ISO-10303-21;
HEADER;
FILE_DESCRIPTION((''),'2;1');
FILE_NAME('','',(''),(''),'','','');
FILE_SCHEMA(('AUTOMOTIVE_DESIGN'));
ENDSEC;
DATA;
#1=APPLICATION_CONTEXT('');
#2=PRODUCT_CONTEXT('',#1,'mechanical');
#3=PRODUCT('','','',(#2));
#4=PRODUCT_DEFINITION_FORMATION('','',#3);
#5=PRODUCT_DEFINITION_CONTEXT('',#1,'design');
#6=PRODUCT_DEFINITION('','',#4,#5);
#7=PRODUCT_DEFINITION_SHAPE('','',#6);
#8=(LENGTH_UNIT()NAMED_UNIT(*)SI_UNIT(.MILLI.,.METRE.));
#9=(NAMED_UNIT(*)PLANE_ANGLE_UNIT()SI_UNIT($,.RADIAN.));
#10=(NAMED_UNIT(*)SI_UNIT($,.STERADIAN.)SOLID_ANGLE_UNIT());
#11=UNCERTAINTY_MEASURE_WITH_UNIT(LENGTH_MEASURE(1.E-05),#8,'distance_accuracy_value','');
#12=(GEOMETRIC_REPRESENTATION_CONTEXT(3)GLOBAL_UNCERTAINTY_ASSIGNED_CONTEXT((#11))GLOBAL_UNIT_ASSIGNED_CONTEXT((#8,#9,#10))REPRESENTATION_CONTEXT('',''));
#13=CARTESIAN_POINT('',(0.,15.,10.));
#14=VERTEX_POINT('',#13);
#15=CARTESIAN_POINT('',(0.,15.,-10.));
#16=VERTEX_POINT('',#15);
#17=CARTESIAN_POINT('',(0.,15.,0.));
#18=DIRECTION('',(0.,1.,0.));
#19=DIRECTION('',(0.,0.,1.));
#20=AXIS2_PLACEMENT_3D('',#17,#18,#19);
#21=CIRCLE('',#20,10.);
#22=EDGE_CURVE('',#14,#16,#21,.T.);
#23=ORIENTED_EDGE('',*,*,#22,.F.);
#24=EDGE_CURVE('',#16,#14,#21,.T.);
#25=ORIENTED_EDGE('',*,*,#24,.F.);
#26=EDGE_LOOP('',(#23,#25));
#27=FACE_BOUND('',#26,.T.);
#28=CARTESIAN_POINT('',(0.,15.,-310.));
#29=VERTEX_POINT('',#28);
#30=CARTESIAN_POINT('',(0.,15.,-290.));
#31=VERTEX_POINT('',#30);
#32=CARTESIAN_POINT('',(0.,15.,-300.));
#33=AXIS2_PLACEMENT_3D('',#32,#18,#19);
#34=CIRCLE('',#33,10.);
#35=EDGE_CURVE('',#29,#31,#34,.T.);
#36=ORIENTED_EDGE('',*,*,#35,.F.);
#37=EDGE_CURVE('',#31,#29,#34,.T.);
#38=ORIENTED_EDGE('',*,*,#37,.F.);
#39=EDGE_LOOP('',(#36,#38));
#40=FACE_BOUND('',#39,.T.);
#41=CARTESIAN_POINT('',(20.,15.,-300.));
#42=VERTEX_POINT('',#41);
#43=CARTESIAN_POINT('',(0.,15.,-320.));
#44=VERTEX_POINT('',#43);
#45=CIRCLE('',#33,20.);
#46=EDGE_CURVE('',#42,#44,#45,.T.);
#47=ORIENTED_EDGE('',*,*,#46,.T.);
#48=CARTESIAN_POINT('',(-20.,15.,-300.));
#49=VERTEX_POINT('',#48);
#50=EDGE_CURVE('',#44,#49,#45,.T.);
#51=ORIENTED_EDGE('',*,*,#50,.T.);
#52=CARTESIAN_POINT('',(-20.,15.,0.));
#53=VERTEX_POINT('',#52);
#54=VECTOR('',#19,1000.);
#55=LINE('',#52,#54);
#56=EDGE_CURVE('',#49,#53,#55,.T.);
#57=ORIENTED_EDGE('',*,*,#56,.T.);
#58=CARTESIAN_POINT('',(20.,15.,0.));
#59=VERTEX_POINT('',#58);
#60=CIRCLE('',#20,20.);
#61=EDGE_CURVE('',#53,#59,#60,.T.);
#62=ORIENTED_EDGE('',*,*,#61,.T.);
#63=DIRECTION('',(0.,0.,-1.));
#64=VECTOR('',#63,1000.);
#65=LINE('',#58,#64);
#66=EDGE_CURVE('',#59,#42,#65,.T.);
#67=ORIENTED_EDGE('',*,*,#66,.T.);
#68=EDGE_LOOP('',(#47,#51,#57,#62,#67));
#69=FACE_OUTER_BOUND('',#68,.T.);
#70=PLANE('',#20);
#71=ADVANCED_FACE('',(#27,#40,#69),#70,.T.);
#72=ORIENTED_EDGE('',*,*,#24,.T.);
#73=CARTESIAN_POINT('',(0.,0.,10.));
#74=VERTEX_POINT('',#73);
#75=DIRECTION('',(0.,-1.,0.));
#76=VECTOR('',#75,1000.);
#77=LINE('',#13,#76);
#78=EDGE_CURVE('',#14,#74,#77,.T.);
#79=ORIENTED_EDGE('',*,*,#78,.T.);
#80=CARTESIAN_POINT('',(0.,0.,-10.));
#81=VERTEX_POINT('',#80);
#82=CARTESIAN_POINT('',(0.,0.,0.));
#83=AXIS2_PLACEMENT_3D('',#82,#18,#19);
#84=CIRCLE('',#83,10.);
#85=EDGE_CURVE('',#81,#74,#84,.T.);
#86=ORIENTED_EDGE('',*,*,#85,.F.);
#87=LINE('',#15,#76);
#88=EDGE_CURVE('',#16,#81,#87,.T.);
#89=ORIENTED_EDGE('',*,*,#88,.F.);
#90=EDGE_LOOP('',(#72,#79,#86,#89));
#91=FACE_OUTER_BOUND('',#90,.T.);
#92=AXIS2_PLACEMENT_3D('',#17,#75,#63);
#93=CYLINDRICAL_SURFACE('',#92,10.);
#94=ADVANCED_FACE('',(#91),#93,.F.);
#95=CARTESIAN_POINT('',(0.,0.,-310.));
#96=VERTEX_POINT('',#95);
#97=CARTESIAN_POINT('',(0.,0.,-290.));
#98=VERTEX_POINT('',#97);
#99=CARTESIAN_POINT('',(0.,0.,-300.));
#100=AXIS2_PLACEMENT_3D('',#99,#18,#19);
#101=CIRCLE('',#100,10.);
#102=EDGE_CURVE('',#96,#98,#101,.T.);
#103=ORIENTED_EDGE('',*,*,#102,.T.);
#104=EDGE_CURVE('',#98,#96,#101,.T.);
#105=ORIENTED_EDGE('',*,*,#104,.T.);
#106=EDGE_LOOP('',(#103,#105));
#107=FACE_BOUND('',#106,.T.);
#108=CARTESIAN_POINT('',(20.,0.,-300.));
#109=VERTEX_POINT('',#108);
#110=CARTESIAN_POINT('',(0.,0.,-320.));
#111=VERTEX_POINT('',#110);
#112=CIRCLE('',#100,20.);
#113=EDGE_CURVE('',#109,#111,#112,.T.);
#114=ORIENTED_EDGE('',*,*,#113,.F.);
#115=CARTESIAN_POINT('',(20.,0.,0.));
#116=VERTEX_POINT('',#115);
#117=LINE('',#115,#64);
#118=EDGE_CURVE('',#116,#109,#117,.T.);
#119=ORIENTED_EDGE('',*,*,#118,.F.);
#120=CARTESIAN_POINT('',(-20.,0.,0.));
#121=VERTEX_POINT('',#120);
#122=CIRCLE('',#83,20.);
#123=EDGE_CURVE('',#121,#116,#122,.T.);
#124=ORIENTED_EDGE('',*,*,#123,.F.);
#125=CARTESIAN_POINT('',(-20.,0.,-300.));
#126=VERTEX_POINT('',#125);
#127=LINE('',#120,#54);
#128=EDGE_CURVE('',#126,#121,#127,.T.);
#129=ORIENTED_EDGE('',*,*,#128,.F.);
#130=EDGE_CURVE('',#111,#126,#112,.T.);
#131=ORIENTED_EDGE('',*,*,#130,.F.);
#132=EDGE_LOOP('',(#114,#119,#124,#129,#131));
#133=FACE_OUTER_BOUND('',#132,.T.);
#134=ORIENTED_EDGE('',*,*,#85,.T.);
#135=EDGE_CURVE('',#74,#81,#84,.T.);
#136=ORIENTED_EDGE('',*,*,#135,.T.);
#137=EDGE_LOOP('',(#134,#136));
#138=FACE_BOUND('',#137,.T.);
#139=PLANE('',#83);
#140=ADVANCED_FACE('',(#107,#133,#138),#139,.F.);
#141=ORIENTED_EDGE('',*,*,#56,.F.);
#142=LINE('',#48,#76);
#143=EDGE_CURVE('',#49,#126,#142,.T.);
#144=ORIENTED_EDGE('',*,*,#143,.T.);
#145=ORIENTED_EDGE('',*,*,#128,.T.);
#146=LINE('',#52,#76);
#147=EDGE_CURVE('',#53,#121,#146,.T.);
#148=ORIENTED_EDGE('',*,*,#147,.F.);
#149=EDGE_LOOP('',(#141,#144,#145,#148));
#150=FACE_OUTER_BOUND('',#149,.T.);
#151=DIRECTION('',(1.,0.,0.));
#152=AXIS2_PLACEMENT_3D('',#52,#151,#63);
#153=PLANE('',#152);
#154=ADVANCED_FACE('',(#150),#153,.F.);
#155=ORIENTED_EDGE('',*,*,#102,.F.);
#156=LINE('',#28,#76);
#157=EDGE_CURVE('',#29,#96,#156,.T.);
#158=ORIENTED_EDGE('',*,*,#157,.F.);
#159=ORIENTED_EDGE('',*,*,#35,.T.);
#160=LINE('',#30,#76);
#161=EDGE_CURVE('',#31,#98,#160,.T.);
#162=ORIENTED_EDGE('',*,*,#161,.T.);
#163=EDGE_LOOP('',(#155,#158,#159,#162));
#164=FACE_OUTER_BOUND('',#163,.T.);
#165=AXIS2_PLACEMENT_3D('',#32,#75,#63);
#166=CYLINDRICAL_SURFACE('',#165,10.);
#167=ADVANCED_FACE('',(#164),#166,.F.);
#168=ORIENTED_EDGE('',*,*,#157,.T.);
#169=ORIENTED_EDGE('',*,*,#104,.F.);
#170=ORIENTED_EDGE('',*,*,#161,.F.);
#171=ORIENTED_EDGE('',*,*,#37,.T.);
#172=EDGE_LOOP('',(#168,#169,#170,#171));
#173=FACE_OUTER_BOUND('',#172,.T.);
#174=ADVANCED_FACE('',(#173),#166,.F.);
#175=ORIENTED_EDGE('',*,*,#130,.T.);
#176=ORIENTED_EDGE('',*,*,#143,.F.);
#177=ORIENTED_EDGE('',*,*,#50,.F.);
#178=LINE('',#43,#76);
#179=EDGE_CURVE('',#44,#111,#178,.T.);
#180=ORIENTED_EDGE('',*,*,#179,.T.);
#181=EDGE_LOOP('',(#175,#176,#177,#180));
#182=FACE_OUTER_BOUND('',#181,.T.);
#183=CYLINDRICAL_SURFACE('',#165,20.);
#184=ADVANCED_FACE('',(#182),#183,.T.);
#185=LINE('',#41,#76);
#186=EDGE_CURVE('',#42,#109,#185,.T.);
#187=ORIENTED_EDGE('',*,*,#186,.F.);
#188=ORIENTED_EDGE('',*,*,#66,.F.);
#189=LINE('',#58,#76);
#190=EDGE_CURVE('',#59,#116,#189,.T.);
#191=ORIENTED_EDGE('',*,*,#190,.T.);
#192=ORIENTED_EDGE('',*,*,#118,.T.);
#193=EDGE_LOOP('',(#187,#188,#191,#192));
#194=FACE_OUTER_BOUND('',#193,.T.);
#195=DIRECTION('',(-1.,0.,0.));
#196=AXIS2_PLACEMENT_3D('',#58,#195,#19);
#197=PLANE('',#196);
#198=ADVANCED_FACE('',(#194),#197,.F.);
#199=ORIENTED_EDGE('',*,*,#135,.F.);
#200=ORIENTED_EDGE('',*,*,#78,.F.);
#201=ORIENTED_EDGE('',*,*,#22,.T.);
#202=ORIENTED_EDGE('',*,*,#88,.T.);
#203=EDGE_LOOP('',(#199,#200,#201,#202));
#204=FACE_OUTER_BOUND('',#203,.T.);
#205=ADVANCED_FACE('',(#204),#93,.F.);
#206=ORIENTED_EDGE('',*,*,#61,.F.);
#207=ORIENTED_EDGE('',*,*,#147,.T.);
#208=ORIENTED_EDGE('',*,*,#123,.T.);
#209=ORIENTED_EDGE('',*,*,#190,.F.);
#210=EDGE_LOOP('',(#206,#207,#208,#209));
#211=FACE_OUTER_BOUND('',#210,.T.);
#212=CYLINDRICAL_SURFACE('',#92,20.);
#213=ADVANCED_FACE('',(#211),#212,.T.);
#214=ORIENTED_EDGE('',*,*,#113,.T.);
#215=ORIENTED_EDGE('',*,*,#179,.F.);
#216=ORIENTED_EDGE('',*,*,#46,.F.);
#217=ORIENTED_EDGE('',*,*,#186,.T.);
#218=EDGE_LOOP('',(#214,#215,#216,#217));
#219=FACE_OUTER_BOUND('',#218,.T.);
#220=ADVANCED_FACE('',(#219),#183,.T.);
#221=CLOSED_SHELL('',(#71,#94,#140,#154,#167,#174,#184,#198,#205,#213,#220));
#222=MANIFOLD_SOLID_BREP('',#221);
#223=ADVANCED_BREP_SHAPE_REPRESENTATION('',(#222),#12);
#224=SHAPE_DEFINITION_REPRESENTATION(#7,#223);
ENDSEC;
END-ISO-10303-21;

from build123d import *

# Parameters (mm, degrees)
SKETCH1_R           = 10
BOSS_EXTRUDE1_DEPTH = 15


with BuildPart() as part:
    # Sketch1 → Boss-Extrude1 (new body)
    with BuildSketch(Plane(origin=(0, 0, 0), x_dir=(1, 0, 0), z_dir=(0, 1, 0))):
        with BuildLine():
            Line((-20, 0), (-20, 300))
            ThreePointArc((-20, 300), (0, 320), (20, 300))
            Line((20, 300), (20, 0))
            ThreePointArc((20, 0), (0, -20), (-20, 0))
        make_face()
        with Locations(Location((0, 300, 0), (0, 0, 270))):
            Circle(SKETCH1_R, mode=Mode.SUBTRACT)
        with Locations(Location((0, 0, 0), (0, 0, 270))):
            Circle(SKETCH1_R, mode=Mode.SUBTRACT)
    extrude(amount=BOSS_EXTRUDE1_DEPTH)


solid = part.part
